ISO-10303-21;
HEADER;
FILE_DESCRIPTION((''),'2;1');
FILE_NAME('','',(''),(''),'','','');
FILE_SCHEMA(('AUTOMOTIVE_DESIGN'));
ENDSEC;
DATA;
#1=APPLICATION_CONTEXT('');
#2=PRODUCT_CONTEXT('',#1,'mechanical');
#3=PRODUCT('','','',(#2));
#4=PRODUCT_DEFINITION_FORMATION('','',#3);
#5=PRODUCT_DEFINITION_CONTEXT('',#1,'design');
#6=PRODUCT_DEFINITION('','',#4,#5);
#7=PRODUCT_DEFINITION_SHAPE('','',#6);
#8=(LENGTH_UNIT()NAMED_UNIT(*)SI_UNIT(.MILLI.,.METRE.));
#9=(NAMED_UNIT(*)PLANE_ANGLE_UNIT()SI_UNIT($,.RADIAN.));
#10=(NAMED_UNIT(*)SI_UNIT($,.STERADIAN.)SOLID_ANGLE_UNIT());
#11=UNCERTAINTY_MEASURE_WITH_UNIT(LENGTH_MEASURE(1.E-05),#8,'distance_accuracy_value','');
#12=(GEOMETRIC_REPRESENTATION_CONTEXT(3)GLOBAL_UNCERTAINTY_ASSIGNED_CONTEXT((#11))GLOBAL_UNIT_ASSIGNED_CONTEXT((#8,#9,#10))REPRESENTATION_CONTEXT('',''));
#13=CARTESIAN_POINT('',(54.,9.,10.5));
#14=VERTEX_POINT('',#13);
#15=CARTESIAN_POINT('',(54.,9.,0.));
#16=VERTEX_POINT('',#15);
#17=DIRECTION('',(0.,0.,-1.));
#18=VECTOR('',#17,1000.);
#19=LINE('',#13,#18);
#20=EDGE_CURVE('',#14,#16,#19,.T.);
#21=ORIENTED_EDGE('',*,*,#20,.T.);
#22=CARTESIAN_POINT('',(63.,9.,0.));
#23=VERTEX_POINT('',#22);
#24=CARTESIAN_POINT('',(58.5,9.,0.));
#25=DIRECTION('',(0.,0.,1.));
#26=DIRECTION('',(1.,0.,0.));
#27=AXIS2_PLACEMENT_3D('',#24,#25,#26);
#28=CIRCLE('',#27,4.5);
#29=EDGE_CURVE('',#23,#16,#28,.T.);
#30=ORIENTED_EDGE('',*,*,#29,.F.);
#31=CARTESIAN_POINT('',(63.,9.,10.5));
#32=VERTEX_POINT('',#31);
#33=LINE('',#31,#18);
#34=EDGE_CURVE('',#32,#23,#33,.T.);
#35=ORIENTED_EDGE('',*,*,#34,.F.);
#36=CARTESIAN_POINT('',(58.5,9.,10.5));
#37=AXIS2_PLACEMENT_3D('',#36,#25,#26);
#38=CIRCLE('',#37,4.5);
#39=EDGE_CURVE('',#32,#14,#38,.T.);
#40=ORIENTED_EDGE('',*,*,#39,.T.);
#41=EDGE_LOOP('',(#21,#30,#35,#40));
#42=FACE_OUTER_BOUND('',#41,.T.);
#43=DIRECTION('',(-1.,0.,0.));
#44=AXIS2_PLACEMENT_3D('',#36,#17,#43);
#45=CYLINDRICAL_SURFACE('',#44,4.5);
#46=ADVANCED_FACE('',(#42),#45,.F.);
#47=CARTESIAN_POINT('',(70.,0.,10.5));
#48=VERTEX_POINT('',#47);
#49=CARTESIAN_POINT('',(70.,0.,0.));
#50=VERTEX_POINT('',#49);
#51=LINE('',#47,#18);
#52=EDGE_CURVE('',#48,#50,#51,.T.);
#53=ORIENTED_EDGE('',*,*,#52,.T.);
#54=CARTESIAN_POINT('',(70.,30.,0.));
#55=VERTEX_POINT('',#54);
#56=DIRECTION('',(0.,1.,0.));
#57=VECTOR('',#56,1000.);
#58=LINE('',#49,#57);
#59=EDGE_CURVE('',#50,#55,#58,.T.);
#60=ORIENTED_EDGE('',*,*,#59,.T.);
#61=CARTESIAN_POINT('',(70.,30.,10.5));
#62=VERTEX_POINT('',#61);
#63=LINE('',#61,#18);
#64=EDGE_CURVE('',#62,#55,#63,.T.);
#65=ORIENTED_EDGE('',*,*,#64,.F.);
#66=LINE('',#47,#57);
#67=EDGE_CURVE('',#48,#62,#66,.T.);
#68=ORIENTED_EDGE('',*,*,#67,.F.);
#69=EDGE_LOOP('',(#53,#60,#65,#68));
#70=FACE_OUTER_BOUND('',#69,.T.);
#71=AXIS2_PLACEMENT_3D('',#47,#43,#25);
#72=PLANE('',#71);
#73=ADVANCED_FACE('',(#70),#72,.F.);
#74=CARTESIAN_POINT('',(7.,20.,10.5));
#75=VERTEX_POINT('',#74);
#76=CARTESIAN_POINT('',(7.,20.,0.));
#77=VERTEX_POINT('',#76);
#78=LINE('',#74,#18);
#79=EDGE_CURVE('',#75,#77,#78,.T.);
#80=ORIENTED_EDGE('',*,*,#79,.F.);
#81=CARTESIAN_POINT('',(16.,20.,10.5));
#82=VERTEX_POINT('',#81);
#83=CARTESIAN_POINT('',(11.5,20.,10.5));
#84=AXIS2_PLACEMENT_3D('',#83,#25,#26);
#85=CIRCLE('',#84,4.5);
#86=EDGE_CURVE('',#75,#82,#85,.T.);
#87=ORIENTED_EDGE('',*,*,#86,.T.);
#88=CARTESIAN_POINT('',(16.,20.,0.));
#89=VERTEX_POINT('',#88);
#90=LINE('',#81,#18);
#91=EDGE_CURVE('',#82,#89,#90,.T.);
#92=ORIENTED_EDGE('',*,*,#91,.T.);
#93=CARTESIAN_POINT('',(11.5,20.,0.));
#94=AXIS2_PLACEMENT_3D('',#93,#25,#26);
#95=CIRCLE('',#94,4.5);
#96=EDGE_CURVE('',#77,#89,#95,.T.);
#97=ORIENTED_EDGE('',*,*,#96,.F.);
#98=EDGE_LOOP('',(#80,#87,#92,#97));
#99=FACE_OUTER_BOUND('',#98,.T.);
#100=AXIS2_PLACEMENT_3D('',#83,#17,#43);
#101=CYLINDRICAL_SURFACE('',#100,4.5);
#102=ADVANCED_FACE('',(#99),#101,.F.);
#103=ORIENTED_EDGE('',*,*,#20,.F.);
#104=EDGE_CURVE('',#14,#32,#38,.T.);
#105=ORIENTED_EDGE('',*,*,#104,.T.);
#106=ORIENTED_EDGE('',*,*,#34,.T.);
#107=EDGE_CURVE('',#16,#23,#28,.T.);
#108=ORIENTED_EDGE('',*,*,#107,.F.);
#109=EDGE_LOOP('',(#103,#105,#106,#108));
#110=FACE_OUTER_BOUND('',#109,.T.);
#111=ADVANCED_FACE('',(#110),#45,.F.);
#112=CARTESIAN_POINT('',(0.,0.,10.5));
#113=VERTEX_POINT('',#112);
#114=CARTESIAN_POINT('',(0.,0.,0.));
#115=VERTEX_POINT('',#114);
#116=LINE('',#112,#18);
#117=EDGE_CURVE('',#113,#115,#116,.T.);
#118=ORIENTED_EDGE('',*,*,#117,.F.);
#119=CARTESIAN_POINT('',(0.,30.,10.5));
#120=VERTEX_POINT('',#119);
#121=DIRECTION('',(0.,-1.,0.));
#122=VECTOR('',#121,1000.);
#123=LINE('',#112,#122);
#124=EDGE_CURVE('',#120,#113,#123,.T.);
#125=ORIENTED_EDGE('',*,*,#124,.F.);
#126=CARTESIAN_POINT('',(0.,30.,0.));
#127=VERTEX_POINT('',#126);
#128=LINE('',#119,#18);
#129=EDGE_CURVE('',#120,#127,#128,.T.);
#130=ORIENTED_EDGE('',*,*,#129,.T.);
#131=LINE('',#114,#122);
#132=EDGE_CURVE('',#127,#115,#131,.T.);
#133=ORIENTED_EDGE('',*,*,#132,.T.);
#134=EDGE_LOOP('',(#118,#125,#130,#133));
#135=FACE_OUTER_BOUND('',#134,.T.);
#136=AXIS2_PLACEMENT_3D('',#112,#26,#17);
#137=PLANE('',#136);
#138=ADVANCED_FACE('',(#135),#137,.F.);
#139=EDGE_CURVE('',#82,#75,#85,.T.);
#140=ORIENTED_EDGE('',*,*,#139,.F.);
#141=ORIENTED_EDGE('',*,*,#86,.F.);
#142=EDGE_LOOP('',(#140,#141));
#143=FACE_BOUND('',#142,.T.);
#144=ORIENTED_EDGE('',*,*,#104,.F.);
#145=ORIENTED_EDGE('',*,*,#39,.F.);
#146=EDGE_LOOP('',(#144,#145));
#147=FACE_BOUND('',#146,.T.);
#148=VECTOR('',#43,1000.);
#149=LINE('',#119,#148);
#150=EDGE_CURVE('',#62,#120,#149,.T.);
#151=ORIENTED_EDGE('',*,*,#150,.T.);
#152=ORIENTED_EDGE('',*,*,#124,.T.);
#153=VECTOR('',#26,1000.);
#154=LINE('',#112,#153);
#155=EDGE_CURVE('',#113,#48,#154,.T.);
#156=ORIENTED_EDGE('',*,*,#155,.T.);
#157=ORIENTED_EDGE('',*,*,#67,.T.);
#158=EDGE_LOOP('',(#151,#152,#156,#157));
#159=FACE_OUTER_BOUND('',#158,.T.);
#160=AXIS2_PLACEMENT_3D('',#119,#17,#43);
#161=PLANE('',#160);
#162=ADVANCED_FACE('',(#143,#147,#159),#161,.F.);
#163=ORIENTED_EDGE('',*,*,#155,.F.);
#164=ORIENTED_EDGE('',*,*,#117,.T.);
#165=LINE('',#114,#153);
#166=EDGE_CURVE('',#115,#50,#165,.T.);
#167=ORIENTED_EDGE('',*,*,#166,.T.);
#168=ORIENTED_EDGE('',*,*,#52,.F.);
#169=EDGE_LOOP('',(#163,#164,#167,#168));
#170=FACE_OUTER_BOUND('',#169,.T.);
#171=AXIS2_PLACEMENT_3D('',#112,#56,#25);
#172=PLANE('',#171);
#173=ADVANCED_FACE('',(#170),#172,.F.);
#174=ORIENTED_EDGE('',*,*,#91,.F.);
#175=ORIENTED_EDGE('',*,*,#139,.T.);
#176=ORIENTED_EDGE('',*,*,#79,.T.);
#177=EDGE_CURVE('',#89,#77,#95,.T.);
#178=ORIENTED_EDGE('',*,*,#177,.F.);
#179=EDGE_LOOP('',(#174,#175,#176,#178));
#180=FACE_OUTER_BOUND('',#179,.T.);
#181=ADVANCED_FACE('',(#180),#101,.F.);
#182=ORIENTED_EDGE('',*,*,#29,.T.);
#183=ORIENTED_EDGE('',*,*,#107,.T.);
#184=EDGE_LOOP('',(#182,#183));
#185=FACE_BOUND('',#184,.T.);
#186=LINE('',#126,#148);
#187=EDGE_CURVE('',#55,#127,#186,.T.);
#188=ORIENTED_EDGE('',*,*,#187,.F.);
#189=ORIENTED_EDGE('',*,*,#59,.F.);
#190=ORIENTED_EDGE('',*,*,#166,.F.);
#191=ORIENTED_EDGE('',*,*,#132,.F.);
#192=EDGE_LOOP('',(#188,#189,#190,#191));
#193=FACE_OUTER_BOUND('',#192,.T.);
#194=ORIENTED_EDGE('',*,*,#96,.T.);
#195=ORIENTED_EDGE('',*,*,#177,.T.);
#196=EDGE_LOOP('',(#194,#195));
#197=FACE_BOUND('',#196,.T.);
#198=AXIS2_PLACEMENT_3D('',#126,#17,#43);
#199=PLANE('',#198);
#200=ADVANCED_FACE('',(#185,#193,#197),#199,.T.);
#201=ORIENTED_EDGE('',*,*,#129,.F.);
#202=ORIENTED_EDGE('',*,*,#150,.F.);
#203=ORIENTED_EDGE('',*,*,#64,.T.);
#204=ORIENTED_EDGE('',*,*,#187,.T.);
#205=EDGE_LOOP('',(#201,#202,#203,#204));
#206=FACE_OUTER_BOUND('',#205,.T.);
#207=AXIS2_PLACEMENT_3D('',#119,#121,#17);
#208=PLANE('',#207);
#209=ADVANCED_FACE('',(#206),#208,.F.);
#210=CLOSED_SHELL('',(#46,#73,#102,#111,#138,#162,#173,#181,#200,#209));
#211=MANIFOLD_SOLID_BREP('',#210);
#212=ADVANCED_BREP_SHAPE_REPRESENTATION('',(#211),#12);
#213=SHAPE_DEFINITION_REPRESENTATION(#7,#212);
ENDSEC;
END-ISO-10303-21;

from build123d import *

# Parameters (mm, degrees)
SKETCH_1_W      = 70
SKETCH_1_H      = 30
SKETCH_1_R      = 4.5
EXTRUDE_1_DEPTH = 10.5


with BuildPart() as part:
    # 草图1 → 凸台-拉伸1 (new body)
    with BuildSketch(Plane.XY):
        with Locations((35, 15)):
            Rectangle(SKETCH_1_W, SKETCH_1_H)
        with Locations(Location((11.5, 20, 0), (0, 0, 180))):
            Circle(SKETCH_1_R, mode=Mode.SUBTRACT)
        with Locations(Location((58.5, 9, 0), (0, 0, 180))):
            Circle(SKETCH_1_R, mode=Mode.SUBTRACT)
    extrude(amount=EXTRUDE_1_DEPTH)


solid = part.part
